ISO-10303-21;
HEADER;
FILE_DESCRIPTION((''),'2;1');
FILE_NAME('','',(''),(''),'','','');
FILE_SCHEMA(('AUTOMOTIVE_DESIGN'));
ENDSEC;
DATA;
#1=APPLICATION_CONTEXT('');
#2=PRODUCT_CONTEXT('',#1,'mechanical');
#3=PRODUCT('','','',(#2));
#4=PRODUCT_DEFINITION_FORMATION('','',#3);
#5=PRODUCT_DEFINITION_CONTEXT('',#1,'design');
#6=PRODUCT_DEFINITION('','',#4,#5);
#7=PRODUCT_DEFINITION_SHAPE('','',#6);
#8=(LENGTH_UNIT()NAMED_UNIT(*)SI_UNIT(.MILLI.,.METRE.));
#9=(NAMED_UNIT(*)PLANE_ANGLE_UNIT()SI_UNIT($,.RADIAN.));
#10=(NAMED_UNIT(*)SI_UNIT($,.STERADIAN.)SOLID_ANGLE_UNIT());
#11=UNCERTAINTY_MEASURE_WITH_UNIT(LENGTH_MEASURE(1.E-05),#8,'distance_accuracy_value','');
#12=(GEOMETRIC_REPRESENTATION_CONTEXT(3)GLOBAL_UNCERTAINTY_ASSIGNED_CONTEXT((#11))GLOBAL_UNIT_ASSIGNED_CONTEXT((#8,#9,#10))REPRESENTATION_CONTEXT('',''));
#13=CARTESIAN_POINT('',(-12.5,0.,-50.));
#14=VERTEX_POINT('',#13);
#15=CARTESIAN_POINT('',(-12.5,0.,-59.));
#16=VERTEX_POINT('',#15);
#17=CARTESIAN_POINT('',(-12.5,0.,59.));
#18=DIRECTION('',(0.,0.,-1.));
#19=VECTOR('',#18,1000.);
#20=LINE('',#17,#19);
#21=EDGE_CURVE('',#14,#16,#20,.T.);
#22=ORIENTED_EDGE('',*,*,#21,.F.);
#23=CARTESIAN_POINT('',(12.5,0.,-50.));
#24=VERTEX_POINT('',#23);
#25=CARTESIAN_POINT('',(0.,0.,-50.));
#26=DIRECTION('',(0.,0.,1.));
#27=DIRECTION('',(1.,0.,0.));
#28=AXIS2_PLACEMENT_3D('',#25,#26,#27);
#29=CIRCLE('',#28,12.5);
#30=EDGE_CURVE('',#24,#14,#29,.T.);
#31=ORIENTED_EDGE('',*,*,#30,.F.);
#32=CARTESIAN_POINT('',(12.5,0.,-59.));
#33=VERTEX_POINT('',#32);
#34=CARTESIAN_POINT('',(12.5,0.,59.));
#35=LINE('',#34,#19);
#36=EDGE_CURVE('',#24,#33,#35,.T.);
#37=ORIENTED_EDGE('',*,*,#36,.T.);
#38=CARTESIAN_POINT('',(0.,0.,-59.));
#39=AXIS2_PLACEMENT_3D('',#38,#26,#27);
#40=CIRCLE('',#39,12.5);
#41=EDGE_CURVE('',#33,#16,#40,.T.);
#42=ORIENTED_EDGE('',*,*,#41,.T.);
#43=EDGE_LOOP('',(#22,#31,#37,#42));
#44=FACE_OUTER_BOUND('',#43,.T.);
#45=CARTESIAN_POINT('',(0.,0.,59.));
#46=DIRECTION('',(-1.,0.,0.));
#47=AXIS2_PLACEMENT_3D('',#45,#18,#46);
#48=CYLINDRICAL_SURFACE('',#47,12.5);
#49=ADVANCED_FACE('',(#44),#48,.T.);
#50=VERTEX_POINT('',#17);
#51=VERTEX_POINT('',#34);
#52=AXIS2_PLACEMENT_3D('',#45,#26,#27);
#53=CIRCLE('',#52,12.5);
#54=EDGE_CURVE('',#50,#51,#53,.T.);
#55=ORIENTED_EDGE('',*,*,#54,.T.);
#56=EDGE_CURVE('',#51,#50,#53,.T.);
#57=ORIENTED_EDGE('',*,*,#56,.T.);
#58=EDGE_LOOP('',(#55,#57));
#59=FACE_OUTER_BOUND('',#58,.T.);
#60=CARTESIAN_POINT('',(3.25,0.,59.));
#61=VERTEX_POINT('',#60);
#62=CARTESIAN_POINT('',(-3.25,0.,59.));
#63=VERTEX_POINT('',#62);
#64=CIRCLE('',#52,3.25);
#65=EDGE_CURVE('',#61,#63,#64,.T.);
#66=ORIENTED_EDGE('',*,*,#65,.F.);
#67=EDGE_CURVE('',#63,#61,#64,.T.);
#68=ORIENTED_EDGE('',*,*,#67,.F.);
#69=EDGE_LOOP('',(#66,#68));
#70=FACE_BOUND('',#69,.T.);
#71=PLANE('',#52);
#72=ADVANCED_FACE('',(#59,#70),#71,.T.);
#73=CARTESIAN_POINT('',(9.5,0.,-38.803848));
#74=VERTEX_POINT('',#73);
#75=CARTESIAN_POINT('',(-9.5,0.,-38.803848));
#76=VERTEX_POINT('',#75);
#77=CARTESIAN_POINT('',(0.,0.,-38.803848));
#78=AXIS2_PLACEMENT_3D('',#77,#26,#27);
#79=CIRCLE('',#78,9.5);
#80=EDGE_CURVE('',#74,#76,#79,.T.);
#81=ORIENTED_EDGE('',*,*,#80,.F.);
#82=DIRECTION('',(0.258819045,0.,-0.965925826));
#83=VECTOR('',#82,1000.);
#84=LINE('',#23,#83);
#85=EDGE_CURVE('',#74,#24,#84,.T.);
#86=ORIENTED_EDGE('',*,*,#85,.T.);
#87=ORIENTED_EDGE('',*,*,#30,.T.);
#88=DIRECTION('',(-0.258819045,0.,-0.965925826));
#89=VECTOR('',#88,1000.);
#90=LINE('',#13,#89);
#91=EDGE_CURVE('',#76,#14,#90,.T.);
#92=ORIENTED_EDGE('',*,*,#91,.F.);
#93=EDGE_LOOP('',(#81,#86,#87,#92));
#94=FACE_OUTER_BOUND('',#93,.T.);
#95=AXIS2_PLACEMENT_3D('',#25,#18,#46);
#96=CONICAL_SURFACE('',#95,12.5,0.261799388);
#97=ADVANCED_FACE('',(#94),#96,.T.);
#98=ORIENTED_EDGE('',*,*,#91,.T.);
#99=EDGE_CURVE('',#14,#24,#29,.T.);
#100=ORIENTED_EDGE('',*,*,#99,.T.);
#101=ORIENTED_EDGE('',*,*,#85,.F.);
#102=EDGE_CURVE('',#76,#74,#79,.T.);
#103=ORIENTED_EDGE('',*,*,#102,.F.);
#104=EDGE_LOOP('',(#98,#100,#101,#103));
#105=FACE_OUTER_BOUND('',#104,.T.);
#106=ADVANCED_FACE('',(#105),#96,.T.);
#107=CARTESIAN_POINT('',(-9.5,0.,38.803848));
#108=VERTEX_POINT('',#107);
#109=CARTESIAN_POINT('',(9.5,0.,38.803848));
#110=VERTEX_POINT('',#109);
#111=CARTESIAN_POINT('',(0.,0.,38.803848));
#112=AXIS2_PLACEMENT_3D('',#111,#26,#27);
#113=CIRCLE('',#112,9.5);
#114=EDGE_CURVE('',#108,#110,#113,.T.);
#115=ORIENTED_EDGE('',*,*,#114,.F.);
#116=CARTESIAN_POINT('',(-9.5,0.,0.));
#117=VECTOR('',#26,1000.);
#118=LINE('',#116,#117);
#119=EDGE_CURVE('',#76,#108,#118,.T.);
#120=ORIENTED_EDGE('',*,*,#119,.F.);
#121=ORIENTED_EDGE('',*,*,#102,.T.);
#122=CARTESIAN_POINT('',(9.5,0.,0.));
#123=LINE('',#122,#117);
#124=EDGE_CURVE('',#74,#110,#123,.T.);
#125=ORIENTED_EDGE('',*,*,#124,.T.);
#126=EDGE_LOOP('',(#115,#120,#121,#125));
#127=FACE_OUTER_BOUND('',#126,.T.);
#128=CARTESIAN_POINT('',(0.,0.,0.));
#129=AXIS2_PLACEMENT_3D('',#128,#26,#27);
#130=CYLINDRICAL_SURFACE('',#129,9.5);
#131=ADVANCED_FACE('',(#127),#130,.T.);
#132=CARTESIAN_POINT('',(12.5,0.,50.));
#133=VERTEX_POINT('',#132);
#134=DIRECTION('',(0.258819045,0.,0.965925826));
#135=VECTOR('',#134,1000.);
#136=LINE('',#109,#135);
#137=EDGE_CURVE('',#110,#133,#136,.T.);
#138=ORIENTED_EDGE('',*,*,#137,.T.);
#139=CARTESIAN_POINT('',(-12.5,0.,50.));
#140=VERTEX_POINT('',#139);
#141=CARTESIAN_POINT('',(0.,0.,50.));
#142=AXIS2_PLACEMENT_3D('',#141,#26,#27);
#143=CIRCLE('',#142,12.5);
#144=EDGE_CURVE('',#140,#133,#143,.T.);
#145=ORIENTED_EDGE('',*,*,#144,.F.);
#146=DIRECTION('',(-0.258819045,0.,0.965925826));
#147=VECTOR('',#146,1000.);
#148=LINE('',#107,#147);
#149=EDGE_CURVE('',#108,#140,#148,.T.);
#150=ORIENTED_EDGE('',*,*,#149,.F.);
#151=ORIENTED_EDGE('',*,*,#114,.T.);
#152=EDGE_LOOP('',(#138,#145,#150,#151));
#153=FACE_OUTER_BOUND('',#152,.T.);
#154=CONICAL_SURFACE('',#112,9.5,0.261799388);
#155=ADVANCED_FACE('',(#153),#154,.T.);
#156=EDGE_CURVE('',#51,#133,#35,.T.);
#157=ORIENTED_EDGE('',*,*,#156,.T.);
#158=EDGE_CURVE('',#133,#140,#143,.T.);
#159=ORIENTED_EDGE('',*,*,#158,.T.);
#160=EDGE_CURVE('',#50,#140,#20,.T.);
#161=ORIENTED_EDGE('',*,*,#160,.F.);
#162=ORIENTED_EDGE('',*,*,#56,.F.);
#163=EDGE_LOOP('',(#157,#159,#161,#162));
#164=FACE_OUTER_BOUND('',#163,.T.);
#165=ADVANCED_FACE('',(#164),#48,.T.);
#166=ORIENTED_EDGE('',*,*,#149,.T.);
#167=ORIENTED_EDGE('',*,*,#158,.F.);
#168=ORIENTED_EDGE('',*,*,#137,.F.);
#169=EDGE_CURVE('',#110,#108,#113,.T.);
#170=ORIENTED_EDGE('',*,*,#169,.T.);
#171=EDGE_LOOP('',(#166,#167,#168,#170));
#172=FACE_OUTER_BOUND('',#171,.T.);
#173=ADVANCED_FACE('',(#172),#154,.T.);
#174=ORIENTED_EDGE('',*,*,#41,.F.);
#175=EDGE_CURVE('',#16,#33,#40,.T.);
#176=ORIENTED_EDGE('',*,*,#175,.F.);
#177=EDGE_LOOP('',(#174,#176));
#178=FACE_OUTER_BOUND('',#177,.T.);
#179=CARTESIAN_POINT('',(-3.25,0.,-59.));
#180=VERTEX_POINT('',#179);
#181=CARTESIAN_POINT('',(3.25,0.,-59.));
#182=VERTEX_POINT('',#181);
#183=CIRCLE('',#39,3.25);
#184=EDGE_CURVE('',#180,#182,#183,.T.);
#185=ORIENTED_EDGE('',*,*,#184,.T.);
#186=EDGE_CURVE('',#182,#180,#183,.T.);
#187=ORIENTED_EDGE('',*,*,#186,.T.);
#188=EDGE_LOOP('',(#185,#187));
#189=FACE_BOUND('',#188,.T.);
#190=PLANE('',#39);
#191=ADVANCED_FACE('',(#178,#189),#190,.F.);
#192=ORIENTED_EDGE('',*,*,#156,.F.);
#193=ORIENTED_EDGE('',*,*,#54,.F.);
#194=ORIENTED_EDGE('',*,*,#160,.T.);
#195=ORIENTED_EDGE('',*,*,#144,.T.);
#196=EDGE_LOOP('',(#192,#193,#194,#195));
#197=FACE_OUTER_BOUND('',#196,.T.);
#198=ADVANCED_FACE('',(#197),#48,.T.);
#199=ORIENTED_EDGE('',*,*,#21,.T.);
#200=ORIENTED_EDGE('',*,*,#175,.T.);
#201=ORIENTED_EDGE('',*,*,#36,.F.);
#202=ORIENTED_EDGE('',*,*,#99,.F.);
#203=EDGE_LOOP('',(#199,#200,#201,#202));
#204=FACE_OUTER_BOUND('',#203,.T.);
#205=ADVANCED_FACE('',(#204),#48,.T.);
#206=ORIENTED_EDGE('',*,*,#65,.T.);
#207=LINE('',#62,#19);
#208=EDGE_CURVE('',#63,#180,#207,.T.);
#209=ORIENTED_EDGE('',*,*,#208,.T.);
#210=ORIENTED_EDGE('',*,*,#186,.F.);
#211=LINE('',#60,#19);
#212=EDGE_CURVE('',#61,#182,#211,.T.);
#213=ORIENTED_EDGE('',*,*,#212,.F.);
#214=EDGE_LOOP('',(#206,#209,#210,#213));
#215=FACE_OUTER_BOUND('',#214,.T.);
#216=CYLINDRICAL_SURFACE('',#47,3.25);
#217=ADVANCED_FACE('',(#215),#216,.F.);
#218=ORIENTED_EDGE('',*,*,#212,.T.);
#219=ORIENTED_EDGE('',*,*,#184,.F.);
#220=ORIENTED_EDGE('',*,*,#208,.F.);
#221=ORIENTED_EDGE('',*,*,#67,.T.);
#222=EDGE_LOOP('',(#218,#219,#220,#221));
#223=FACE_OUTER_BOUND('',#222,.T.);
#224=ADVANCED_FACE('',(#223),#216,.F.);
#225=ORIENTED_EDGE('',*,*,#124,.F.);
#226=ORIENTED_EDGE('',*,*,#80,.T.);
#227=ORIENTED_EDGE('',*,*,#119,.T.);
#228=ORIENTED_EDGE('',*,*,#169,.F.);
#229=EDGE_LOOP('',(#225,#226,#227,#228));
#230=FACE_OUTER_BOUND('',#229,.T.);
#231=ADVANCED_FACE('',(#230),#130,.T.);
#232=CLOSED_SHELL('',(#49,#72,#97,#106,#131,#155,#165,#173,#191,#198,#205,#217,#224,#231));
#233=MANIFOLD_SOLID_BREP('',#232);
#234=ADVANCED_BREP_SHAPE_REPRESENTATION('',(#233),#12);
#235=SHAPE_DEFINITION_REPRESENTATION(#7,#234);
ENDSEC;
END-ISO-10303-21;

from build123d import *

# Parameters (mm, degrees)
SKETCH1_R           = 12.5
SKETCH1_R_2         = 3.25
BOSS_EXTRUDE1_DEPTH = 59


with BuildPart() as part:
    # Sketch1 → Boss-Extrude1 (new, symmetric)
    with BuildSketch(Plane.XY):
        Circle(SKETCH1_R)
        Circle(SKETCH1_R_2, mode=Mode.SUBTRACT)
    extrude(amount=BOSS_EXTRUDE1_DEPTH, both=True)

    # Sketch3 → Cut-Revolve1 (revolve, cut)
    with BuildSketch(Plane(origin=(0, 0, 0), x_dir=(1, 0, 0), z_dir=(0, 1, 0))):
        Polygon((12.5, -50), (12.5, 50), (9.5, 38.803847577), (9.5, -38.803847577), align=None)
    revolve(axis=Axis((0, 0, 0), (0, 0, -1)), mode=Mode.SUBTRACT)


solid = part.part
